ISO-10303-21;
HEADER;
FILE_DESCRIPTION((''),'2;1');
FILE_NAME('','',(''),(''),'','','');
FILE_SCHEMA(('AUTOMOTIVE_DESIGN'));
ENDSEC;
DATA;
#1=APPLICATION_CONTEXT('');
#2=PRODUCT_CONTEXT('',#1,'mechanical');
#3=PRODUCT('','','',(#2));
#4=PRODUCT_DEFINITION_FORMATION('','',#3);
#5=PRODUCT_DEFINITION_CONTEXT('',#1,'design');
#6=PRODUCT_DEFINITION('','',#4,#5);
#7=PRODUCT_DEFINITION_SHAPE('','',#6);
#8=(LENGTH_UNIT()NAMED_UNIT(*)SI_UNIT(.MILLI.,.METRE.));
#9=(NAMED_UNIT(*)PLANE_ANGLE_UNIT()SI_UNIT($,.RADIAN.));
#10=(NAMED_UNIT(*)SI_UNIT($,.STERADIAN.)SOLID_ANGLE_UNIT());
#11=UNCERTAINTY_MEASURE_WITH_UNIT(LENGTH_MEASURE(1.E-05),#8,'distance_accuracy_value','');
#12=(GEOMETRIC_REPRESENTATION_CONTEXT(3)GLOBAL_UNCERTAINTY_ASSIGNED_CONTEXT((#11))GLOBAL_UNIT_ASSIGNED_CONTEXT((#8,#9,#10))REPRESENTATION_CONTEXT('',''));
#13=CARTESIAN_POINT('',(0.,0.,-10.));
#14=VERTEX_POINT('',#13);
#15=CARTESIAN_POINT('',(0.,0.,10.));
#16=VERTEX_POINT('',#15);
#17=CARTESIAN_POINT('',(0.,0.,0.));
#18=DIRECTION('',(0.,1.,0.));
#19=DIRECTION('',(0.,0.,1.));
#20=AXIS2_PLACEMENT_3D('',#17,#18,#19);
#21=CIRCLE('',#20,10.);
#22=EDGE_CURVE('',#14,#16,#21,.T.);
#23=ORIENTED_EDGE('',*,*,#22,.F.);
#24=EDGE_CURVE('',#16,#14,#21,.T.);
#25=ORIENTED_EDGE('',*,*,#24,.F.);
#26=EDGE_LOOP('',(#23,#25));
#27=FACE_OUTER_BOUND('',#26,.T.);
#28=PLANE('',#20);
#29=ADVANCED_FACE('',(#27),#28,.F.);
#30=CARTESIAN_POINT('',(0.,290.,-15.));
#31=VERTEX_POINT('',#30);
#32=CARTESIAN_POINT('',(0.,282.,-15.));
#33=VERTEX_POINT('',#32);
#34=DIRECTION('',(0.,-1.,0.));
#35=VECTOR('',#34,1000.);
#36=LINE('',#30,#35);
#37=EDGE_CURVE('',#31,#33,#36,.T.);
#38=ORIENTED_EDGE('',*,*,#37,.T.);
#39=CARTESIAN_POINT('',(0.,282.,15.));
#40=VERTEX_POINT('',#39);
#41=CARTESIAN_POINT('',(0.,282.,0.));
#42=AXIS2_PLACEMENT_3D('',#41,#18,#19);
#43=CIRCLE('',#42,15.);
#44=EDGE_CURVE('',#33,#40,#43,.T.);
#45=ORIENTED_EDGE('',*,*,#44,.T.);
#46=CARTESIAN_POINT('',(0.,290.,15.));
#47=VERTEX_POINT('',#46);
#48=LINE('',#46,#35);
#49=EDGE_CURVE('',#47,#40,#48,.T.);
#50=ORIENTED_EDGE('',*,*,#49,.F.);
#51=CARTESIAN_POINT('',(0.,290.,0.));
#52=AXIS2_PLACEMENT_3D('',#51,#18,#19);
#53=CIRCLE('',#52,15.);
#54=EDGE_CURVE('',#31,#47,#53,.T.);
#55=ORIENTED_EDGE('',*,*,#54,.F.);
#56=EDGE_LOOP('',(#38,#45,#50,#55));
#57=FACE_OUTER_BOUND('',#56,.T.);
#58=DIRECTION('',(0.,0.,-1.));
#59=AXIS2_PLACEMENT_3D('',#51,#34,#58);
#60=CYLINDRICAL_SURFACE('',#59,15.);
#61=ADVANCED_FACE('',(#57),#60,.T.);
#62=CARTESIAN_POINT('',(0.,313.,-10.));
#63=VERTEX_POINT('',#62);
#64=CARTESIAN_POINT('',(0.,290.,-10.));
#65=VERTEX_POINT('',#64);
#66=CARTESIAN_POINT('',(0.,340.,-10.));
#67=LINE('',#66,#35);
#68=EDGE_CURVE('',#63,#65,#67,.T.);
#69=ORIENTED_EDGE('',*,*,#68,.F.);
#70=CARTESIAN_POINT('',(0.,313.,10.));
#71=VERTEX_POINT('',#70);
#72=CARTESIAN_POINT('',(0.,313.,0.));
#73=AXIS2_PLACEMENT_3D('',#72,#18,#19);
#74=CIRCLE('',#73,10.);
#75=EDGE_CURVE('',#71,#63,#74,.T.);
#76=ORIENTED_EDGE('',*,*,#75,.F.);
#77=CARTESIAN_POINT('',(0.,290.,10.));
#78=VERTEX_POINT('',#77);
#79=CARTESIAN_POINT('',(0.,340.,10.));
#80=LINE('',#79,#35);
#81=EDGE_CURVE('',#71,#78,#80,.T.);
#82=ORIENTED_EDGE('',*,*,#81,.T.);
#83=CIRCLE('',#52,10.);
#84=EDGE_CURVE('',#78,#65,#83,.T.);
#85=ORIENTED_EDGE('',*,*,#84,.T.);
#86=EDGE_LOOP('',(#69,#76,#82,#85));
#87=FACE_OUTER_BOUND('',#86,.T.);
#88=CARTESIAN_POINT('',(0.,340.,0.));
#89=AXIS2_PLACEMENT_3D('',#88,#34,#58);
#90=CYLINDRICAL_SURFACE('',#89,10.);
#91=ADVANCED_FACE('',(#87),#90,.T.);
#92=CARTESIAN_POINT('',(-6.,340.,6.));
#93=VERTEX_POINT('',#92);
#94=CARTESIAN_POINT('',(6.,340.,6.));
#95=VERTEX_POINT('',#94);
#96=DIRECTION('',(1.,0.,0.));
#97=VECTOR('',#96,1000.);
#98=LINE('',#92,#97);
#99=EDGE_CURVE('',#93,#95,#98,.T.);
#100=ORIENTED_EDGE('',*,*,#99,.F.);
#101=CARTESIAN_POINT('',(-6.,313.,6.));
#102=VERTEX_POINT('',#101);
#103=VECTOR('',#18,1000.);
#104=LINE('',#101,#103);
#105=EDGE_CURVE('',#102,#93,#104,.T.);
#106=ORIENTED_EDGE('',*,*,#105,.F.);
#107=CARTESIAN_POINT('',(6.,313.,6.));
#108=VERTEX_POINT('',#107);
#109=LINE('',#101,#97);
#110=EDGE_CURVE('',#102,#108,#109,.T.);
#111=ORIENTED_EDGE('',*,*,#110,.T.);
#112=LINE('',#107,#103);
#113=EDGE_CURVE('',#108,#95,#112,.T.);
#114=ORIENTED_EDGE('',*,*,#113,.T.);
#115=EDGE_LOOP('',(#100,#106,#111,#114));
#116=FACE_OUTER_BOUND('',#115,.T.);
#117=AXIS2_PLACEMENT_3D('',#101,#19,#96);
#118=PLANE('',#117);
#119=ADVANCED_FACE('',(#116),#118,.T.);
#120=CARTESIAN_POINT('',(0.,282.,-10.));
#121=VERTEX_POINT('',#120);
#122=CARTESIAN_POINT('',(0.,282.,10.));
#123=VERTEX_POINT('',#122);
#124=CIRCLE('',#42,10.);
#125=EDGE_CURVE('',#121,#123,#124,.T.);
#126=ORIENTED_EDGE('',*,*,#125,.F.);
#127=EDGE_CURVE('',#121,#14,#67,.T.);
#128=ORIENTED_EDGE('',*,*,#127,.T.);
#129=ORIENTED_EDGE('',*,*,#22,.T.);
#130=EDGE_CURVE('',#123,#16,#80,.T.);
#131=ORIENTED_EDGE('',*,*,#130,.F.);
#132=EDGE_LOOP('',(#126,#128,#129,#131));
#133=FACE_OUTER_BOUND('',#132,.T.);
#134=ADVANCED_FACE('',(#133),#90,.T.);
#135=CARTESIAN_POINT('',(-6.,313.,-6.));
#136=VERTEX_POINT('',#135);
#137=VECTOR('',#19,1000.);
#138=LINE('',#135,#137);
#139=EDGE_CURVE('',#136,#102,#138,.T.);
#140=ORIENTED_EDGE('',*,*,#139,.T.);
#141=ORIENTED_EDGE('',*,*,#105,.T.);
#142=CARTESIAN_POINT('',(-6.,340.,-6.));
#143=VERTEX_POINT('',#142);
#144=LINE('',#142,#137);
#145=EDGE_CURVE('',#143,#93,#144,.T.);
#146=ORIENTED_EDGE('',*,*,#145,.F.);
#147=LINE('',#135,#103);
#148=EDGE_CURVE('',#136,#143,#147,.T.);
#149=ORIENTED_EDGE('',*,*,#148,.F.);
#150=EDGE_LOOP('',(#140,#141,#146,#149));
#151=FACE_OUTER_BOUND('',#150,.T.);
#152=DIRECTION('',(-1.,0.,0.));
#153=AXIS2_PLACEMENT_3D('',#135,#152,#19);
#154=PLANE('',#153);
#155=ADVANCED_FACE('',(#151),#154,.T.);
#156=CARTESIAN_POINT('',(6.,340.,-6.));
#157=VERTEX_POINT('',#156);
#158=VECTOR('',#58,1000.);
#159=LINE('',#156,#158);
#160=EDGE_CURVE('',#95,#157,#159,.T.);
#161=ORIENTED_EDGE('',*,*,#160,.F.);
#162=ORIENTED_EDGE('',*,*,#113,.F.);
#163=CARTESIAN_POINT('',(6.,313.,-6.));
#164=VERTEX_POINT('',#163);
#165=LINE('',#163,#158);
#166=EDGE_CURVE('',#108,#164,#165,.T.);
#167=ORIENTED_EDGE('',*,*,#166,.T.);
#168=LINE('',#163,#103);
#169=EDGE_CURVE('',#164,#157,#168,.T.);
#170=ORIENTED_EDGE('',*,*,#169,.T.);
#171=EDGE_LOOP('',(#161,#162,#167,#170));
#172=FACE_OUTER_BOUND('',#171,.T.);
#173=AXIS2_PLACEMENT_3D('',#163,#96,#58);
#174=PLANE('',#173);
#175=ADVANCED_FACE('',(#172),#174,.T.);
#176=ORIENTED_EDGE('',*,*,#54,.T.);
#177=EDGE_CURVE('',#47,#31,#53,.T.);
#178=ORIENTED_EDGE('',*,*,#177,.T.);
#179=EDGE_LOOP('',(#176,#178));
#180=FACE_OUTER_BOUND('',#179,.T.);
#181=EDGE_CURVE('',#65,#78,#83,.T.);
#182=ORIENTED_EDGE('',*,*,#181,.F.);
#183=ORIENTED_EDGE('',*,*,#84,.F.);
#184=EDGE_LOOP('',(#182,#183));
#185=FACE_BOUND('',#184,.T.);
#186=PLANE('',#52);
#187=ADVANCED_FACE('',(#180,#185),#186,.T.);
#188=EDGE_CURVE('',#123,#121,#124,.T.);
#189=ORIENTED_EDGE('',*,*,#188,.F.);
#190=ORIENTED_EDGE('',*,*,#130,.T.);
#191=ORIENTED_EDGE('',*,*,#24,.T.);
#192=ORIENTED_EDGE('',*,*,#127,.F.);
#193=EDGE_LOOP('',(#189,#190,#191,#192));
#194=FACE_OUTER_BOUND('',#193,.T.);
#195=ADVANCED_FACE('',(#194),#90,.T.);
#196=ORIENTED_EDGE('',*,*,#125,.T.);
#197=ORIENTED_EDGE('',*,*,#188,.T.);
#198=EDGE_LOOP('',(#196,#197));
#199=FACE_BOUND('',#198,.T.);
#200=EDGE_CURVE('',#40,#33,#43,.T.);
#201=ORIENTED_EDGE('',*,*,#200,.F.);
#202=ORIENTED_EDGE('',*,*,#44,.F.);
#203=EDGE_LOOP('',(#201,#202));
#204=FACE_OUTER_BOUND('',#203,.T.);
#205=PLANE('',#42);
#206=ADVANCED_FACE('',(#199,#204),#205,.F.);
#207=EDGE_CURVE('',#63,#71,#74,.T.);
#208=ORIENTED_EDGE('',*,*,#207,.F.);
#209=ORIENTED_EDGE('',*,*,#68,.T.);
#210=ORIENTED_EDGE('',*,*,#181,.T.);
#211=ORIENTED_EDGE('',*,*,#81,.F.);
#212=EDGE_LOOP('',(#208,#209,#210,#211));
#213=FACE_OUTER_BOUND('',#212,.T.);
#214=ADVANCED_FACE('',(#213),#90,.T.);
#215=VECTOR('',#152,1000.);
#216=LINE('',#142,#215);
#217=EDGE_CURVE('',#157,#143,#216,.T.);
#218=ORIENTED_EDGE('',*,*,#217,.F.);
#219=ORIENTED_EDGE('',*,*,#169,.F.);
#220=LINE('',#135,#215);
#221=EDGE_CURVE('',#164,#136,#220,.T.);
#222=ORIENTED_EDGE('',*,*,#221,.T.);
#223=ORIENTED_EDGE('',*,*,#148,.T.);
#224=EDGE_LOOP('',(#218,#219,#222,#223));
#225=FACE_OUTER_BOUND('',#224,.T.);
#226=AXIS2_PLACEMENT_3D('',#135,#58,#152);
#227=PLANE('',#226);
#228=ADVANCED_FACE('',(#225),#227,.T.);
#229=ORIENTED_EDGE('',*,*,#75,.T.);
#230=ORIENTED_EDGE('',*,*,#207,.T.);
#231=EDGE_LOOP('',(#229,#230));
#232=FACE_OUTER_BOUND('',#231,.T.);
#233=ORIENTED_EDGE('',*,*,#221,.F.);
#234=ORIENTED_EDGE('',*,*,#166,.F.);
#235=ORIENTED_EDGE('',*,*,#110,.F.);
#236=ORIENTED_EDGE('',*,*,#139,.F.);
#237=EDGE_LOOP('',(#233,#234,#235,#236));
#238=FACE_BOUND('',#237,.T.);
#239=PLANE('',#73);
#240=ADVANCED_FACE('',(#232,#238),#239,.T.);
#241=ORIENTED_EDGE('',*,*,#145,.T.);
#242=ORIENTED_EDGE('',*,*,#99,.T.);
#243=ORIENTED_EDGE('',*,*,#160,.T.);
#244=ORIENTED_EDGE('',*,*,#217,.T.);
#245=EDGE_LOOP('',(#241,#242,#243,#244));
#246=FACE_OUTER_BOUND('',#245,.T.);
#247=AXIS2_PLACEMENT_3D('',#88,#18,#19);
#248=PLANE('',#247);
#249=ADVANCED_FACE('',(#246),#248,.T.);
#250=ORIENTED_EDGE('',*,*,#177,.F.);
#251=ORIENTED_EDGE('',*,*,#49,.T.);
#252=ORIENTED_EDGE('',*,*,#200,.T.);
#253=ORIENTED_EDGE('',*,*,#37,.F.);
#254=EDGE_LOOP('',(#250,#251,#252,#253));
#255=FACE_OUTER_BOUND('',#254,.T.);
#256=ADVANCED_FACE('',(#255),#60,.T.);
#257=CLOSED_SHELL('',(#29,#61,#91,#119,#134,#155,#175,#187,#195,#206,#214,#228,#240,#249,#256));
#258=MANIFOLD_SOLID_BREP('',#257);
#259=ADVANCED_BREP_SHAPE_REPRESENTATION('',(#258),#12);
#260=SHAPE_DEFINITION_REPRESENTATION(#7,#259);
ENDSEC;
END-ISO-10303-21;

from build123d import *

# Parameters (mm, degrees)
SKETCH1_R           = 10
BOSS_EXTRUDE1_DEPTH = 340
SKETCH2_OUTSIDE_W   = 90.234
SKETCH2_OUTSIDE_H   = 90.234
SKETCH2_OUTSIDE_W_2 = 12
SKETCH2_OUTSIDE_H_2 = 12
CUT_EXTRUDE1_DEPTH  = 27
SKETCH3_R           = 15
BOSS_EXTRUDE2_DEPTH = 8


with BuildPart() as part:
    # Sketch1 → Boss-Extrude1 (new body)
    with BuildSketch(Plane(origin=(0, 0, 0), x_dir=(1, 0, 0), z_dir=(0, 1, 0))):
        with Locations(Location((0, 0, 0), (0, 0, 270))):
            Circle(SKETCH1_R)
    extrude(amount=BOSS_EXTRUDE1_DEPTH)

    # Sketch2 outside → Cut-Extrude1 (cut)
    with BuildSketch(Plane(origin=(0, 340, 0), x_dir=(1, 0, 0), z_dir=(0, 1, 0))):
        Rectangle(SKETCH2_OUTSIDE_W, SKETCH2_OUTSIDE_H)
        Rectangle(SKETCH2_OUTSIDE_W_2, SKETCH2_OUTSIDE_H_2, mode=Mode.SUBTRACT)
    extrude(amount=-CUT_EXTRUDE1_DEPTH, mode=Mode.SUBTRACT)

    # Sketch3 → Boss-Extrude2 (add)
    with BuildSketch(Plane(origin=(0, 282, 0), x_dir=(1, 0, 0), z_dir=(0, 1, 0))):
        with Locations(Location((0, 0, 0), (0, 0, 270))):
            Circle(SKETCH3_R)
    extrude(amount=BOSS_EXTRUDE2_DEPTH)


solid = part.part
